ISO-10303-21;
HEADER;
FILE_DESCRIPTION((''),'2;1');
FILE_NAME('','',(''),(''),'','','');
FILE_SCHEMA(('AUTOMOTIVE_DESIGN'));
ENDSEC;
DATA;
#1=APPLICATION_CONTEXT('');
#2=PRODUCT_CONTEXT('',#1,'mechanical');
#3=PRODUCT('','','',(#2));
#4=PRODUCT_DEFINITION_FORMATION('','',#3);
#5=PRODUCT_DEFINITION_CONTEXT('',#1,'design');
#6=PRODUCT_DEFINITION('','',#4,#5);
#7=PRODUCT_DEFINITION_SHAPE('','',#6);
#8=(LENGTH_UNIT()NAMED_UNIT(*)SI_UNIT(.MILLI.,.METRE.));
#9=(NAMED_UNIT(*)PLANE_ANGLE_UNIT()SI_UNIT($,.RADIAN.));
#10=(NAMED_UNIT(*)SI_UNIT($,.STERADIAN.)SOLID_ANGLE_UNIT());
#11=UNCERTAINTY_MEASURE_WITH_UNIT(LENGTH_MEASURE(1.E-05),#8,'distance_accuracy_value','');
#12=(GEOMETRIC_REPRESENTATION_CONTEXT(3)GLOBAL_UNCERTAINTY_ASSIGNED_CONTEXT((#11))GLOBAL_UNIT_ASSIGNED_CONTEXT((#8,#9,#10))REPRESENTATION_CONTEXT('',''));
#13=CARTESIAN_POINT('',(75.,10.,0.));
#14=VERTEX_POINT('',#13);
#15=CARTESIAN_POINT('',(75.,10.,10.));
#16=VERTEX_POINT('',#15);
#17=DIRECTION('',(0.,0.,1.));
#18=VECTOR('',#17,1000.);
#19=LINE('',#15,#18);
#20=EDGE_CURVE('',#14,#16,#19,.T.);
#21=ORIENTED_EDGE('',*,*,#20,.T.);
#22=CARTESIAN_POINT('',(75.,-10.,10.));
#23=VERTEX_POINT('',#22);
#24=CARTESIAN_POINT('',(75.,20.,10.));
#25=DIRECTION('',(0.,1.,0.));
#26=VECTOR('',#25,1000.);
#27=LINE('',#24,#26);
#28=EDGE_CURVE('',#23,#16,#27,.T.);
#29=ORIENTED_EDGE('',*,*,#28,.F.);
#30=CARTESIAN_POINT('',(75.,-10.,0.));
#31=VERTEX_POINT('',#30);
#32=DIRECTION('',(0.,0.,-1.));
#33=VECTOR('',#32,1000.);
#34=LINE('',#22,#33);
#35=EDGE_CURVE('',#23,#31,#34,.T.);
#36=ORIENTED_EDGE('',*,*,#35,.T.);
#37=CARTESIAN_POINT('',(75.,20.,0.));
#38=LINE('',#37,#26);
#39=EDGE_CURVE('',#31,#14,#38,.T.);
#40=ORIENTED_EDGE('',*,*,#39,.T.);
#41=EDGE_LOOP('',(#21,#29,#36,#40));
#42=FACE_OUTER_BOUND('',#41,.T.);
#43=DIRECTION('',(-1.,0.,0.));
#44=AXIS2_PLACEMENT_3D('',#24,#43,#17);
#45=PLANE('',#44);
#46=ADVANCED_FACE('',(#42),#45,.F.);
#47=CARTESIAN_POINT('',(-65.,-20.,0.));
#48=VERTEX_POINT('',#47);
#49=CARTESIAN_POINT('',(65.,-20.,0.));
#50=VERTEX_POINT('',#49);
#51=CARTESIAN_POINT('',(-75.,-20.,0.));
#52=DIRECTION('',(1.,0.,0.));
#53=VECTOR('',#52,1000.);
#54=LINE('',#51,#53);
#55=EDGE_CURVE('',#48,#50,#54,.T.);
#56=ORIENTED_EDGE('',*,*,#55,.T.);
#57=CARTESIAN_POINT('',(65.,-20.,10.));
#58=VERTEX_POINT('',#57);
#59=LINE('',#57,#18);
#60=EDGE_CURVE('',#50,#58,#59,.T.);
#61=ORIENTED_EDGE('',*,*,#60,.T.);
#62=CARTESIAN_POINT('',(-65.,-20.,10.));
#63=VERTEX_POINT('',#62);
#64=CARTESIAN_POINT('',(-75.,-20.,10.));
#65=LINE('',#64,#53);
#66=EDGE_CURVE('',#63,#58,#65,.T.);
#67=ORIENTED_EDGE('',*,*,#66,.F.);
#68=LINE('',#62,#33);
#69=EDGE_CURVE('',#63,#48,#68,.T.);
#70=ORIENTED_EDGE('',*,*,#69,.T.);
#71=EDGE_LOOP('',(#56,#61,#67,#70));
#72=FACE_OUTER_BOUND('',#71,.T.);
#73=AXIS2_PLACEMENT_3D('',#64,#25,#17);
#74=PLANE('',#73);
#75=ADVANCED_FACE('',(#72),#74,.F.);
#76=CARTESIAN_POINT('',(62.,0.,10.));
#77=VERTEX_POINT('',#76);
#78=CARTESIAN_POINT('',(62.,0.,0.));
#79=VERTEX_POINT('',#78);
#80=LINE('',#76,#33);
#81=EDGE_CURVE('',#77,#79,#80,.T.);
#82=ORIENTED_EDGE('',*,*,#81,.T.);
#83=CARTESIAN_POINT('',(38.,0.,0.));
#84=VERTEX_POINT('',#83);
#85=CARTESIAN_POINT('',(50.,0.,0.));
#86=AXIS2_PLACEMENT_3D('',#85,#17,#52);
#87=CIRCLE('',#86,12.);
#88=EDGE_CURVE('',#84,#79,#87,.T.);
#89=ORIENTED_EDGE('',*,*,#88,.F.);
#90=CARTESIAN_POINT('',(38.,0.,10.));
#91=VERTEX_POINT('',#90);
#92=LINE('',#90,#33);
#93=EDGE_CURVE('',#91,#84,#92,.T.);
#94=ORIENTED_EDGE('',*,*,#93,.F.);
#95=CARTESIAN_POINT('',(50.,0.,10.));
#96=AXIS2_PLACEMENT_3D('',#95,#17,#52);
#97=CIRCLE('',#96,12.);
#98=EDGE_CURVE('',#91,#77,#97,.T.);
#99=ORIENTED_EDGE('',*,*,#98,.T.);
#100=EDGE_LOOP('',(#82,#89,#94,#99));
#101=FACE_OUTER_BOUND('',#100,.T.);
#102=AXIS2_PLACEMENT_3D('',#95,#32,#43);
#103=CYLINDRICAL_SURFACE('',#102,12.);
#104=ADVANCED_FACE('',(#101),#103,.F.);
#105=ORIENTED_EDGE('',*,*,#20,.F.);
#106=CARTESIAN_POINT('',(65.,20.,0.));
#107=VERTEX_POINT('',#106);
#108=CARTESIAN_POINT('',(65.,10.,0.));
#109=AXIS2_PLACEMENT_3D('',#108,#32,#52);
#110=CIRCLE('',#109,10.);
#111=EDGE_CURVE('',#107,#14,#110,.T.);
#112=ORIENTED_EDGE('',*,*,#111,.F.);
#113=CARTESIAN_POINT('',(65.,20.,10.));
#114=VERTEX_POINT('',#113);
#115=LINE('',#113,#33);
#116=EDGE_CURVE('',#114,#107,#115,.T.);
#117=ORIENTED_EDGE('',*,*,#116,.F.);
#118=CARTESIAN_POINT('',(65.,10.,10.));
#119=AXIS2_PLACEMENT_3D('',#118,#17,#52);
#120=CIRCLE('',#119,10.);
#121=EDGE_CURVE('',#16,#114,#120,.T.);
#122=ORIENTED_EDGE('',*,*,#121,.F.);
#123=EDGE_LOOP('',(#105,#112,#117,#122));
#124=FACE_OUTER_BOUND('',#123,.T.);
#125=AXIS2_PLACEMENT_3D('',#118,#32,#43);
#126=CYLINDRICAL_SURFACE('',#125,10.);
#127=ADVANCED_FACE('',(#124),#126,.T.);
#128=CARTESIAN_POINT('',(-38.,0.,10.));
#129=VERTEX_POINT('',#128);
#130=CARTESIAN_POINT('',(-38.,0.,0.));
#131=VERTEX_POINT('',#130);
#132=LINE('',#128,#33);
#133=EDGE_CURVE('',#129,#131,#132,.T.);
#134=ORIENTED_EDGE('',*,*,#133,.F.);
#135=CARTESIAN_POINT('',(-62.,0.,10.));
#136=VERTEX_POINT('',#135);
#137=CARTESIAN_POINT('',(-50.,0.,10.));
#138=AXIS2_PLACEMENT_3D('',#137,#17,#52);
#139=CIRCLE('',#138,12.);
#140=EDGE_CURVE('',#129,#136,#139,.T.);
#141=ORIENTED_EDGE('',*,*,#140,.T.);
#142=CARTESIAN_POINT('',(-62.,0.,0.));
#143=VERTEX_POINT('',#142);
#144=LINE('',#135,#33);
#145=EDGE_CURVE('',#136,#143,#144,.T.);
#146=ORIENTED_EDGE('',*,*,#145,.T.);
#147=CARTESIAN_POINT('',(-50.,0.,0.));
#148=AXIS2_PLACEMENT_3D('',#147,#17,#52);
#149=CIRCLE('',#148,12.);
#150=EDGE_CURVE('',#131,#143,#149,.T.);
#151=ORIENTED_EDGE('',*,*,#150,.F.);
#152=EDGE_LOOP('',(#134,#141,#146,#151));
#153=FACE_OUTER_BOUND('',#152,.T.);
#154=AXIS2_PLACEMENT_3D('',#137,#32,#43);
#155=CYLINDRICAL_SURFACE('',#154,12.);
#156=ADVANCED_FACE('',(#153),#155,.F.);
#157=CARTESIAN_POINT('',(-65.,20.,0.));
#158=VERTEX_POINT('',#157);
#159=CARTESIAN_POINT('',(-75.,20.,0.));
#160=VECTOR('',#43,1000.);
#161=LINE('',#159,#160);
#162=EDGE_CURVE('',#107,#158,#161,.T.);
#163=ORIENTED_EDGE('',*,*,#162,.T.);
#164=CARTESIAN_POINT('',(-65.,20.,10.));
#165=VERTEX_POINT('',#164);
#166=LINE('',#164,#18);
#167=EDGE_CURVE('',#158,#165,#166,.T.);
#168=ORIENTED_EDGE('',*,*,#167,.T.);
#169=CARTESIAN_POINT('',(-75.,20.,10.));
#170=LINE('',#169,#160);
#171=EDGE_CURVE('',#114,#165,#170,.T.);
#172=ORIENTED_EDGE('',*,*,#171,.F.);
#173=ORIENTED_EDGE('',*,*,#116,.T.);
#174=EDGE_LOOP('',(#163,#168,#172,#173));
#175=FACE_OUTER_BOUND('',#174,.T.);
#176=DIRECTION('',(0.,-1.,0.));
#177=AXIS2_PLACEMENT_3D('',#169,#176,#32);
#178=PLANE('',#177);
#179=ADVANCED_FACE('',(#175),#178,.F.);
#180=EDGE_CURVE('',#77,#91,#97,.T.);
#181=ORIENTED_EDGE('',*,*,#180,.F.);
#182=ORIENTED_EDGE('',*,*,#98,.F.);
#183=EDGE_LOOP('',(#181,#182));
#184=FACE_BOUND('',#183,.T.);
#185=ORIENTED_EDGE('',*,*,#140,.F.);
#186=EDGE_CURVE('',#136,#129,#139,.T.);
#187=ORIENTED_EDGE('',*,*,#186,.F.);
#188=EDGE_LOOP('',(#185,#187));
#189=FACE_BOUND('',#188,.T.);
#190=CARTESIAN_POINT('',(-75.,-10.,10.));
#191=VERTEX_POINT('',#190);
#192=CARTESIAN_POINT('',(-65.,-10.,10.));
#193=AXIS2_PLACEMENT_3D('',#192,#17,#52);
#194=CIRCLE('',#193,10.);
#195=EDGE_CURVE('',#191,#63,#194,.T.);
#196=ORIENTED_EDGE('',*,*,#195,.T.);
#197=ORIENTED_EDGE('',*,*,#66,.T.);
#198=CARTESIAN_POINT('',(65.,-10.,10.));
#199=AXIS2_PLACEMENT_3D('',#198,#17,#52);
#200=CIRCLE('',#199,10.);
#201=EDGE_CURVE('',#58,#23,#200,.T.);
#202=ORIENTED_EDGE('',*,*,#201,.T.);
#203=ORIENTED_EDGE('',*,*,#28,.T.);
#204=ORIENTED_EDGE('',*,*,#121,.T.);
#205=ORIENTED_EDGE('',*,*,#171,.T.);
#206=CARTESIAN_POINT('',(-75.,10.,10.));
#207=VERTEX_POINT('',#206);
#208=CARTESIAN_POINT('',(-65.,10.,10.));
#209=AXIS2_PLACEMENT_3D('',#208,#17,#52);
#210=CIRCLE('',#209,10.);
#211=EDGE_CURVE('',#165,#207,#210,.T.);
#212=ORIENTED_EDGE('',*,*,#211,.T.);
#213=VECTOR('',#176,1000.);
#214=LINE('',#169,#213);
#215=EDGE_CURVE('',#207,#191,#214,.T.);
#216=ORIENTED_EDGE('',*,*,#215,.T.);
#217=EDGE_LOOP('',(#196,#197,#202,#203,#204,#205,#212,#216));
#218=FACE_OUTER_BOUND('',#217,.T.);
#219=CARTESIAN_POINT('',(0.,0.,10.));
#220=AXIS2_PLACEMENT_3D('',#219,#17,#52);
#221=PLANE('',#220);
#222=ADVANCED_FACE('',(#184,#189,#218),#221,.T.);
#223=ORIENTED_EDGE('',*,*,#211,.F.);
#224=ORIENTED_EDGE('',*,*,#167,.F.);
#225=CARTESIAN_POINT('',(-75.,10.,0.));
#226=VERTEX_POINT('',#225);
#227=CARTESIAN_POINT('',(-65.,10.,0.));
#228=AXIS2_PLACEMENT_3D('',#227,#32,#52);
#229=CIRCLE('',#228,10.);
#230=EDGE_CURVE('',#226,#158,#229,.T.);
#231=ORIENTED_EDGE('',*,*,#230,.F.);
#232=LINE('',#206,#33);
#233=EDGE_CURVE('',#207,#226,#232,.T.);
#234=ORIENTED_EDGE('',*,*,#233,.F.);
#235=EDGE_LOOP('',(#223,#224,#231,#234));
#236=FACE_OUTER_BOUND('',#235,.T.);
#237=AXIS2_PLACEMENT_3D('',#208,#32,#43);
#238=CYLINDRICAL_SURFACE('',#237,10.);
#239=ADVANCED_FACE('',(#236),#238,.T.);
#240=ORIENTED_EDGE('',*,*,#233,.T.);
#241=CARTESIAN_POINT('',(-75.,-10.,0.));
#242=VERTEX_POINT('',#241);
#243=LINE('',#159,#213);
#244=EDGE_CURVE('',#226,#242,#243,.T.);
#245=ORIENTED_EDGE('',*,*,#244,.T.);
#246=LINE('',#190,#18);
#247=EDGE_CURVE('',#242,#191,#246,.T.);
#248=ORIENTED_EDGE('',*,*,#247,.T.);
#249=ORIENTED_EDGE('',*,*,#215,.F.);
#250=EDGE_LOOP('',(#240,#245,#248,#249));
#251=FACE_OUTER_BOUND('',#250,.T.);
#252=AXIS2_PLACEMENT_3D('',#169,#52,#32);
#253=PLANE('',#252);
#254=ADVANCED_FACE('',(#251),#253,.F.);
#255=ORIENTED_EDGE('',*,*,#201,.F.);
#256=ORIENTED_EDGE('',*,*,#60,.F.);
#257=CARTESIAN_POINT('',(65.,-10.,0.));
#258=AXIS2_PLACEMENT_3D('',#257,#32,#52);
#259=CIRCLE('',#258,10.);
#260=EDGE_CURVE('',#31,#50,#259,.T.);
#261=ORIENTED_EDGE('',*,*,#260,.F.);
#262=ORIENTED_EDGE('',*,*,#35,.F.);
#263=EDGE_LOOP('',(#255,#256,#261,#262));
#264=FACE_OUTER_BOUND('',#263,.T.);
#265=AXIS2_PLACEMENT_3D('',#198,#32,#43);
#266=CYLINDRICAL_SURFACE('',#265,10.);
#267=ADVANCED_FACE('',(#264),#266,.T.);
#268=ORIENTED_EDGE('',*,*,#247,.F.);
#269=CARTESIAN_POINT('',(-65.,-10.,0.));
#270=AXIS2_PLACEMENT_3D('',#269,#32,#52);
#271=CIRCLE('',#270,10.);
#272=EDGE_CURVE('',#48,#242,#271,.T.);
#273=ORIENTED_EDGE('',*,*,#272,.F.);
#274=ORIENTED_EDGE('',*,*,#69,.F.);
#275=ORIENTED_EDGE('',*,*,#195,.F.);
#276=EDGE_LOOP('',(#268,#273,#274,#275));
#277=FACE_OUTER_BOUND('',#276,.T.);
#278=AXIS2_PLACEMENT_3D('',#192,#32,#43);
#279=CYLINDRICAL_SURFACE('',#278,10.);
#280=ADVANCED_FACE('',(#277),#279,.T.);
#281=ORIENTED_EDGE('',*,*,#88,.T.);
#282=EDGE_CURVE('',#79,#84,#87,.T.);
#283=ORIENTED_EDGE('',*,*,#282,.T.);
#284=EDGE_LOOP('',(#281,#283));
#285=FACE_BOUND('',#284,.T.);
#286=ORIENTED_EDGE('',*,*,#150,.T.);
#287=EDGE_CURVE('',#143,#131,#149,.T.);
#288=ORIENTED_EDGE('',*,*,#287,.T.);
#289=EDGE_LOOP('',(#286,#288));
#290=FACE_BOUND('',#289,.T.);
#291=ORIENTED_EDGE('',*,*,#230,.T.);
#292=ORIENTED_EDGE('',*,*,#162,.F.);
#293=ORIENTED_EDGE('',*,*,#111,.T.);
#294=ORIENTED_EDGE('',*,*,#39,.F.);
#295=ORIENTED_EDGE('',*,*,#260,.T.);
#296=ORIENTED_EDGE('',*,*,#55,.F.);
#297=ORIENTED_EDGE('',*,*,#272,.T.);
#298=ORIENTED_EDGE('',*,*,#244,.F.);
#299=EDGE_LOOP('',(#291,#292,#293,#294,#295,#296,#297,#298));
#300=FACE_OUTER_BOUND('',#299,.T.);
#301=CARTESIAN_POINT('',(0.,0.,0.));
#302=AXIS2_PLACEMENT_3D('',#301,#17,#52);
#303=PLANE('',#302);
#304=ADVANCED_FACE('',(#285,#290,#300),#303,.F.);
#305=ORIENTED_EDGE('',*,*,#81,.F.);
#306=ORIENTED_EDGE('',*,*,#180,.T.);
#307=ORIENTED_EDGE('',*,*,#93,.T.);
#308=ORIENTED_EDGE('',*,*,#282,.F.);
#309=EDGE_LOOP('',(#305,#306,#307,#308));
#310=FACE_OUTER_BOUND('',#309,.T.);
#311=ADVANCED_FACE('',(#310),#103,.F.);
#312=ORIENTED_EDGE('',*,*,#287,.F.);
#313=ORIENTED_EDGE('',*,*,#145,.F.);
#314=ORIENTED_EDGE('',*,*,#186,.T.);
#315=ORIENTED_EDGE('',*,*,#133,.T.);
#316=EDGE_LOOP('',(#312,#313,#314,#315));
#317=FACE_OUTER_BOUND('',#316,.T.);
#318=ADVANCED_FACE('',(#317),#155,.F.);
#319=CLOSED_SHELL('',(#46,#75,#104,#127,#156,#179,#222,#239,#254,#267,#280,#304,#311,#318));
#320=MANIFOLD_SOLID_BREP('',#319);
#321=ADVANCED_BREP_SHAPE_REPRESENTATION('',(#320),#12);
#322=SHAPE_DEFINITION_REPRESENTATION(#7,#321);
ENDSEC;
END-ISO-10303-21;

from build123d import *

# Parameters (mm, degrees)
SKETCH1_W           = 150
SKETCH1_H           = 40
SKETCH1_R           = 12
BOSS_EXTRUDE1_DEPTH = 10
FILLET1_R           = 10


with BuildPart() as part:
    # Sketch1 → Boss-Extrude1 (new body)
    with BuildSketch(Plane.XY):
        Rectangle(SKETCH1_W, SKETCH1_H)
        with Locations((50, 0)):
            Circle(SKETCH1_R, mode=Mode.SUBTRACT)
        with Locations((-50, 0)):
            Circle(SKETCH1_R, mode=Mode.SUBTRACT)
    extrude(amount=BOSS_EXTRUDE1_DEPTH)

    # Fillet1
    fillet1_edges = [part.edges().sort_by_distance(p)[0] for p in [
        (75, -20, 5),
        (-75, -20, 5),
        (-75, 20, 5),
        (75, 20, 5),
    ]]
    fillet(fillet1_edges, radius=FILLET1_R)


solid = part.part
